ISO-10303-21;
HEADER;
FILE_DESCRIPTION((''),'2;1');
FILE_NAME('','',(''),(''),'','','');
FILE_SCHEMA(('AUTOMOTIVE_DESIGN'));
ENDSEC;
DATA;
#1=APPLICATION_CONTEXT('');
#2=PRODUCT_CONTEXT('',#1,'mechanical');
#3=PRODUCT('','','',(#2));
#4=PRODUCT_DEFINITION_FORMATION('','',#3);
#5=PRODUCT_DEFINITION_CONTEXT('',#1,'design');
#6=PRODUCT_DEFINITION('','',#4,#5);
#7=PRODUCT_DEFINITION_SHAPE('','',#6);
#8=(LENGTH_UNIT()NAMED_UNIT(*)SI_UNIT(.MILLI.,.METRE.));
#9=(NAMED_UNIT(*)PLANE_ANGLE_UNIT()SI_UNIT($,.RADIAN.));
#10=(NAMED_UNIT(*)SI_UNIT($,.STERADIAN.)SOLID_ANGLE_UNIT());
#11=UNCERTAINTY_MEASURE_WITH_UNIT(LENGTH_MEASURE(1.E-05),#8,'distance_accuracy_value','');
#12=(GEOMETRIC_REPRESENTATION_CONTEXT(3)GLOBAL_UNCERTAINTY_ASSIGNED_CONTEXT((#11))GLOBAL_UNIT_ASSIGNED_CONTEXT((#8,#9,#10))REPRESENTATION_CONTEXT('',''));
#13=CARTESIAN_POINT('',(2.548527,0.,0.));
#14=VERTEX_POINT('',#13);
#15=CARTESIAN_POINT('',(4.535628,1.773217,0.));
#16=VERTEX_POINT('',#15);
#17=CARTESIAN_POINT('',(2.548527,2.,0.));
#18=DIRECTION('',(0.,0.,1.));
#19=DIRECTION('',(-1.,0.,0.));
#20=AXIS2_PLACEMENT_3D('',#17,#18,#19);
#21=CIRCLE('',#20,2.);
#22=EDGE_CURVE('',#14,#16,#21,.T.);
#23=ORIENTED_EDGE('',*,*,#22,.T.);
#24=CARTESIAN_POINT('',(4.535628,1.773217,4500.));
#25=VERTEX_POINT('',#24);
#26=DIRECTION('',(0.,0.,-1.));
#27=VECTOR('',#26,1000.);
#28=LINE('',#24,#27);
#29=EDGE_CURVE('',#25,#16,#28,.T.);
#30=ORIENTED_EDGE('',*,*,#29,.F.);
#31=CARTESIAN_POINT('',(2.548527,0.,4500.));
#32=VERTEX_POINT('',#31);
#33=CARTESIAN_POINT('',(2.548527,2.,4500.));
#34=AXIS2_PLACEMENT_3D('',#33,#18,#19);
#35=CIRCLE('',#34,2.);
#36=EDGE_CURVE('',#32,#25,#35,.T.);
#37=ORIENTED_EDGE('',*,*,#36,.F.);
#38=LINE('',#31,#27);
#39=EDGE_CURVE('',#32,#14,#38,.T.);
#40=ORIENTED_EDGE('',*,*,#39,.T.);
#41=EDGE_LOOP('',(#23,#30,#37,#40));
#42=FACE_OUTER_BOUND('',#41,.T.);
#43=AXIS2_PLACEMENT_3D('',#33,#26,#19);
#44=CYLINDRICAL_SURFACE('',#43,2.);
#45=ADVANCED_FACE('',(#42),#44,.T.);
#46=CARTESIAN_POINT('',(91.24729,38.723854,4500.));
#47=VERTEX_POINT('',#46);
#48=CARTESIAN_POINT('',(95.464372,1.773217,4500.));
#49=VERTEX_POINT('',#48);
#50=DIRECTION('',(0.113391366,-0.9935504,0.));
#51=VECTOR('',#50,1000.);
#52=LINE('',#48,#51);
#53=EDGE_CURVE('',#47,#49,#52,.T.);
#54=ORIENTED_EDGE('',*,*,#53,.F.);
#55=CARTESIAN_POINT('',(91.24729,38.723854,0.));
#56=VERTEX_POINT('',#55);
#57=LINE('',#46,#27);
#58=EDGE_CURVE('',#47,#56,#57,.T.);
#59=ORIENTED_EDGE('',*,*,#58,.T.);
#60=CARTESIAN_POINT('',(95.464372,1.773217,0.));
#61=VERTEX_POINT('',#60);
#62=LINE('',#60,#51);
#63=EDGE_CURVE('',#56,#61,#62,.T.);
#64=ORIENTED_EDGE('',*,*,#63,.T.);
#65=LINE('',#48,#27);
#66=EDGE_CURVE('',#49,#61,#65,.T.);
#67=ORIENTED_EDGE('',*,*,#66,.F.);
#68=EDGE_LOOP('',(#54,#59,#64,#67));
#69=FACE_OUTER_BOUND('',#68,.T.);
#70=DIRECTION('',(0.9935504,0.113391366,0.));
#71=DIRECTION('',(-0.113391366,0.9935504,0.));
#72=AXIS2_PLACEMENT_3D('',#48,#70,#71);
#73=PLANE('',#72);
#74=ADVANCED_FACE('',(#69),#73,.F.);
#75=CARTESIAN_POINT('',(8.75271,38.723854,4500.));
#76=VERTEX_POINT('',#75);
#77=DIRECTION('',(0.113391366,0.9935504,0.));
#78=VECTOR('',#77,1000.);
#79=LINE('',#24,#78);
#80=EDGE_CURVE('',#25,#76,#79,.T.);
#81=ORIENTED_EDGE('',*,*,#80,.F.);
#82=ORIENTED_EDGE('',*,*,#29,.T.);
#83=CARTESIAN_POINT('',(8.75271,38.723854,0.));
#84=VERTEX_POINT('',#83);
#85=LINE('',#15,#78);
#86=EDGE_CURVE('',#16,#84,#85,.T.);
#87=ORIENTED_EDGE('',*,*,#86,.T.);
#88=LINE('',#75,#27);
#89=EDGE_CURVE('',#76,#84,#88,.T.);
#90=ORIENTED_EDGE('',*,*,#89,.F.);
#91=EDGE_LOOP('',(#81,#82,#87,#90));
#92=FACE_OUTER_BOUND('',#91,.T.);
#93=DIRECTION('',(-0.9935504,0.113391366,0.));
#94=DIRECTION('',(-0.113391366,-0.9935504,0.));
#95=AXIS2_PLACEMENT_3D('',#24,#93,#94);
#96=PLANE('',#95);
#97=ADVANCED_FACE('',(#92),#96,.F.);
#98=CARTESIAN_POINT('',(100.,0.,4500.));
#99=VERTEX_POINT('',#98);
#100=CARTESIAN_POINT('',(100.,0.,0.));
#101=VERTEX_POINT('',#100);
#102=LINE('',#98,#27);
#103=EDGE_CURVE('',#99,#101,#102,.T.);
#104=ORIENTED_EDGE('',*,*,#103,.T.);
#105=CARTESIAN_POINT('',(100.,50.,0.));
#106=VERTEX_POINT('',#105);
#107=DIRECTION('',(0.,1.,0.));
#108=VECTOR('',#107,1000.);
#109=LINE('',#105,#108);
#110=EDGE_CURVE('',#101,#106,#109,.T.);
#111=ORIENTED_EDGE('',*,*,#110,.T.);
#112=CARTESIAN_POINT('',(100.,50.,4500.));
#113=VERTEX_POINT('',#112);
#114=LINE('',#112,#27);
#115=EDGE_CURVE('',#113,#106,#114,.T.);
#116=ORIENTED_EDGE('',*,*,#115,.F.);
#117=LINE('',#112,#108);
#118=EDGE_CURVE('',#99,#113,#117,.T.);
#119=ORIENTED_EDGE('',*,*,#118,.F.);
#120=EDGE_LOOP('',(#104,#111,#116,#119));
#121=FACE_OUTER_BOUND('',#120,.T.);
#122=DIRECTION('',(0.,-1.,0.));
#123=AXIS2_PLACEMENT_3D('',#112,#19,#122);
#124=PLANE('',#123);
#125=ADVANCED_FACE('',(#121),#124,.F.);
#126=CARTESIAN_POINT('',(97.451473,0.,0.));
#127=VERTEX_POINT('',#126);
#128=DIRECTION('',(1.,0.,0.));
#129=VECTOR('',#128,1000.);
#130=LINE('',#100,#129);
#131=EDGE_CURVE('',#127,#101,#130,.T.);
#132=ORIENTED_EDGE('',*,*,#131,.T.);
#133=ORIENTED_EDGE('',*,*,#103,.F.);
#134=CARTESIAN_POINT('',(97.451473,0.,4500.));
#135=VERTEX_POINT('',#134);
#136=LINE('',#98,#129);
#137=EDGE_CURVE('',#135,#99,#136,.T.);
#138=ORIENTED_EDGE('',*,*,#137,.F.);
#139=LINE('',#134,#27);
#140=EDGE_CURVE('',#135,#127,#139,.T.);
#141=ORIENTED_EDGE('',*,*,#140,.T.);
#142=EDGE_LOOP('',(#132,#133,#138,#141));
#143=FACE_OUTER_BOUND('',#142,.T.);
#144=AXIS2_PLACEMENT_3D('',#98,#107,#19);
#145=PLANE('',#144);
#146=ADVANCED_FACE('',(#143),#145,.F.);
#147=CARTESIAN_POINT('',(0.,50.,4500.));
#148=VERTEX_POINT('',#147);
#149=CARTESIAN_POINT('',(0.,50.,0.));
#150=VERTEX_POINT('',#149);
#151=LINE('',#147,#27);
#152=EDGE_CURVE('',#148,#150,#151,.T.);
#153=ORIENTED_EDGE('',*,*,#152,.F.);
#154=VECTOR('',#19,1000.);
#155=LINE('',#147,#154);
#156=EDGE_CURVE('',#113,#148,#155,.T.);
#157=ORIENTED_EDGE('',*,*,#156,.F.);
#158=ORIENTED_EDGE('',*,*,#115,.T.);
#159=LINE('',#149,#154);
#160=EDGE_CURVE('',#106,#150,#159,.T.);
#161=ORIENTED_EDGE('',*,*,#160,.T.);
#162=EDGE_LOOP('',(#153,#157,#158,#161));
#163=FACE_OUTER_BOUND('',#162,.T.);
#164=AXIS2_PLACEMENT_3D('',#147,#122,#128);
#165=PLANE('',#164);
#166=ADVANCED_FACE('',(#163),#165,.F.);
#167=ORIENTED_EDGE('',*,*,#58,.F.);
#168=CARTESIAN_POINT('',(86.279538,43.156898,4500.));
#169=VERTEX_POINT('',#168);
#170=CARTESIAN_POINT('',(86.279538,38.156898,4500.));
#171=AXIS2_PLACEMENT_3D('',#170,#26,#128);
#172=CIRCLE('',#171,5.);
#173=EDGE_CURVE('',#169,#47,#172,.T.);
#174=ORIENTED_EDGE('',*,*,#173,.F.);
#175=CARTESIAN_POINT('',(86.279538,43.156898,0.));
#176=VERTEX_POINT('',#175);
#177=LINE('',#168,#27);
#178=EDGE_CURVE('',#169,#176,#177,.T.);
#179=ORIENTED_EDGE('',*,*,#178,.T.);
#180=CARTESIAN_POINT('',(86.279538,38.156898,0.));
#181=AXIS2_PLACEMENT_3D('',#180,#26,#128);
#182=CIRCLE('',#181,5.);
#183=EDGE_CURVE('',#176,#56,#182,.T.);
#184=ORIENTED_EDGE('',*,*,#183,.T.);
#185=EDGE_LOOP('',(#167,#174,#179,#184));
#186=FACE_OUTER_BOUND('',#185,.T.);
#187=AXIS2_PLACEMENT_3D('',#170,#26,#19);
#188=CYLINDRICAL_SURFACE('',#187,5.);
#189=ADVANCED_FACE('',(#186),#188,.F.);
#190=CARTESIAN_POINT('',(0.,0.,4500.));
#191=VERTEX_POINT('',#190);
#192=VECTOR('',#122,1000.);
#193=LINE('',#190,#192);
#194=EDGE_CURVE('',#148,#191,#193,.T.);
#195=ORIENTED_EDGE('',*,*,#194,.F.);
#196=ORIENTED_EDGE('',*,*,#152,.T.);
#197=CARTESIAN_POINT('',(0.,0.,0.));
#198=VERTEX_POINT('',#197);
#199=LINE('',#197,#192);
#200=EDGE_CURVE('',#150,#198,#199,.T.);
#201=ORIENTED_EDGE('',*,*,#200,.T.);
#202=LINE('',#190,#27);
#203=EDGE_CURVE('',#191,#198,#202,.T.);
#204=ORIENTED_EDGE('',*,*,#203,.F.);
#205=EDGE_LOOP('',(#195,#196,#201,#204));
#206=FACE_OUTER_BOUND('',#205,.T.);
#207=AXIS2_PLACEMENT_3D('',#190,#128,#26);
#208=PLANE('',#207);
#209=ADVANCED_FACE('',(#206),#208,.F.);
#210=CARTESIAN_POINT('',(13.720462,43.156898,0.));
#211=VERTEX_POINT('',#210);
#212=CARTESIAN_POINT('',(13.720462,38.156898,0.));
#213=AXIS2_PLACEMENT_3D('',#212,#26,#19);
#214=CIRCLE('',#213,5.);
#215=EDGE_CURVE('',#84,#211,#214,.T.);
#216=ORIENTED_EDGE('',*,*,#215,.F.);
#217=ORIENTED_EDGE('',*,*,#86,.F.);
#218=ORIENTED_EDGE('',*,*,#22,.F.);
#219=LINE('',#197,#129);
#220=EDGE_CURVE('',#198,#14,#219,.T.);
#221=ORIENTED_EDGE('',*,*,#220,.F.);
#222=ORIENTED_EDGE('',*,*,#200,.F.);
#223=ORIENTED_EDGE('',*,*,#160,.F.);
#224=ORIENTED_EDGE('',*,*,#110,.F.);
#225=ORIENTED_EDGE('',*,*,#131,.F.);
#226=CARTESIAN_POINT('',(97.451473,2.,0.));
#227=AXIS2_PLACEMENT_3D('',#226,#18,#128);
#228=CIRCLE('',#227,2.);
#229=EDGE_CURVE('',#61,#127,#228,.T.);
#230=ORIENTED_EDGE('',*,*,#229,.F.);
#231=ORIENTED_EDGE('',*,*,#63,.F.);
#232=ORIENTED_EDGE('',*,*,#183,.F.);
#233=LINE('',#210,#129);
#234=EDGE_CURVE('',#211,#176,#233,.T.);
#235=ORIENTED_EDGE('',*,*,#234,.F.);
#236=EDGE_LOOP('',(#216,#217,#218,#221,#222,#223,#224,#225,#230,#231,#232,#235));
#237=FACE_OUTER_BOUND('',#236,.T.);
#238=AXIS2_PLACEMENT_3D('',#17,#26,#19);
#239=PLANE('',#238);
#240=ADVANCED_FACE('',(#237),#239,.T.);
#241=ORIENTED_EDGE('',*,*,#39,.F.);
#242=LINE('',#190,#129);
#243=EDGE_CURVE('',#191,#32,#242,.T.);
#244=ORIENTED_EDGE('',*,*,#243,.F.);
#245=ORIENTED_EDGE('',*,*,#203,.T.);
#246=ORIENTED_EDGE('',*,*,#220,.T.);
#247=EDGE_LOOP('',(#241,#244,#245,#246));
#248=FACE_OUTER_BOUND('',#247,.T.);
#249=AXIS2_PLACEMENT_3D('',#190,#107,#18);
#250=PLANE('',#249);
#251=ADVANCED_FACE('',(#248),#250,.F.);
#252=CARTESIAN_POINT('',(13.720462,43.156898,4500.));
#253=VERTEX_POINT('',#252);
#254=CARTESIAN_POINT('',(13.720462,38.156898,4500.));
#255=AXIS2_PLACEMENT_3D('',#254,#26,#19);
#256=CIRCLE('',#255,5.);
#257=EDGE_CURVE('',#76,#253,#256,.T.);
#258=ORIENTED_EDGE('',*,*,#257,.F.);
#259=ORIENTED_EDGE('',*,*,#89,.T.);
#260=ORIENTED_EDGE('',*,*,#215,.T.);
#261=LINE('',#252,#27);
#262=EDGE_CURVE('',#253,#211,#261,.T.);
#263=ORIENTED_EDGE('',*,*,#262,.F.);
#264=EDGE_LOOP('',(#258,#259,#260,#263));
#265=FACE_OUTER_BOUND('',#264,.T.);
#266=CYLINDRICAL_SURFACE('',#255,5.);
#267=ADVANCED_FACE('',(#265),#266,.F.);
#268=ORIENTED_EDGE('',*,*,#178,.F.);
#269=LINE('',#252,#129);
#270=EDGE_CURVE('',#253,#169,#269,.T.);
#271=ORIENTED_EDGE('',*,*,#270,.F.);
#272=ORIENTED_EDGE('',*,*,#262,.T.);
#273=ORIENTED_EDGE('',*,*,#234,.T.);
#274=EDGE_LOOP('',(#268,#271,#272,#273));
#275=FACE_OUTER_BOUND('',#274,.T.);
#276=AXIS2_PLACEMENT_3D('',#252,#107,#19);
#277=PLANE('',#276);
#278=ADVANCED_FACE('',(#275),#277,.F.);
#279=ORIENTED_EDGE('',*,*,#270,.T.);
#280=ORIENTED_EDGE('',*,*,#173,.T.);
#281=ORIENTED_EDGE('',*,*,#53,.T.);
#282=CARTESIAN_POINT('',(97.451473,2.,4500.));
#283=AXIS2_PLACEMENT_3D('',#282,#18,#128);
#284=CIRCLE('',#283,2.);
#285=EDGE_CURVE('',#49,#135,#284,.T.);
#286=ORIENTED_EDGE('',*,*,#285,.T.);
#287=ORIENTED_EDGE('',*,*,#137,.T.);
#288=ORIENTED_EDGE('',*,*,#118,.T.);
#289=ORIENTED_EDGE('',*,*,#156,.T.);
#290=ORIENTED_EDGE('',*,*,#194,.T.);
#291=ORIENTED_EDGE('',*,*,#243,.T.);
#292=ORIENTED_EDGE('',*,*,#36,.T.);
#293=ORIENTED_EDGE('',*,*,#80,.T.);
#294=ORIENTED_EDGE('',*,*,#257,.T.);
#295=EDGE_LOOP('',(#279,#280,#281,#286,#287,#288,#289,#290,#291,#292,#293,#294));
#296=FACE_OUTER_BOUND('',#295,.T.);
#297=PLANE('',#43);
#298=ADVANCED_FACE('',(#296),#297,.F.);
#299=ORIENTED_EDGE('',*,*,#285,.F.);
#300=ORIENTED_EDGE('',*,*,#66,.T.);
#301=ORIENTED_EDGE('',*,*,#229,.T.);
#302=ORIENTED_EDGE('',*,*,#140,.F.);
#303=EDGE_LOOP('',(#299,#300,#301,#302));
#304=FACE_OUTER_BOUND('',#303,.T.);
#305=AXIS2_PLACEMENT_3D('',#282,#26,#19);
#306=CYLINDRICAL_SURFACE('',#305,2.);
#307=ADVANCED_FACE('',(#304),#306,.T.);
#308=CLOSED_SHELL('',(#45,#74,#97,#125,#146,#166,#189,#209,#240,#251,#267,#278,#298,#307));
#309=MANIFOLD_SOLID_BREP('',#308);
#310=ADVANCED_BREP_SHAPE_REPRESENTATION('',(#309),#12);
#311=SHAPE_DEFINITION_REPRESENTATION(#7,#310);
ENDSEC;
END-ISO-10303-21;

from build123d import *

# Parameters (mm, degrees)
BOSS_EXTRUDE1_DEPTH = 4500


with BuildPart() as part:
    # Sketch1 → Boss-Extrude1 (new body)
    with BuildSketch(Plane.XY):
        with BuildLine():
            Line((0, 0), (0, 50))
            Line((0, 50), (100, 50))
            Line((100, 50), (100, 0))
            Line((100, 0), (97.451472673, 0))
            ThreePointArc((97.451472673, 0), (96.119850629, 0.507759157), (95.464371872, 1.773217267))
            Line((95.464371872, 1.773217267), (91.247290138, 38.723854473))
            ThreePointArc((91.247290138, 38.723854473), (89.608593246, 41.887499748), (86.279538137, 43.156897641))
            Line((86.279538137, 43.156897641), (13.720461863, 43.156897641))
            ThreePointArc((13.720461863, 43.156897641), (10.391406754, 41.887499748), (8.752709862, 38.723854473))
            Line((8.752709862, 38.723854473), (4.535628128, 1.773217267))
            ThreePointArc((4.535628128, 1.773217267), (3.880149371, 0.507759157), (2.548527327, 0))
            Line((2.548527327, 0), (0, 0))
        make_face()
    extrude(amount=BOSS_EXTRUDE1_DEPTH)


solid = part.part
